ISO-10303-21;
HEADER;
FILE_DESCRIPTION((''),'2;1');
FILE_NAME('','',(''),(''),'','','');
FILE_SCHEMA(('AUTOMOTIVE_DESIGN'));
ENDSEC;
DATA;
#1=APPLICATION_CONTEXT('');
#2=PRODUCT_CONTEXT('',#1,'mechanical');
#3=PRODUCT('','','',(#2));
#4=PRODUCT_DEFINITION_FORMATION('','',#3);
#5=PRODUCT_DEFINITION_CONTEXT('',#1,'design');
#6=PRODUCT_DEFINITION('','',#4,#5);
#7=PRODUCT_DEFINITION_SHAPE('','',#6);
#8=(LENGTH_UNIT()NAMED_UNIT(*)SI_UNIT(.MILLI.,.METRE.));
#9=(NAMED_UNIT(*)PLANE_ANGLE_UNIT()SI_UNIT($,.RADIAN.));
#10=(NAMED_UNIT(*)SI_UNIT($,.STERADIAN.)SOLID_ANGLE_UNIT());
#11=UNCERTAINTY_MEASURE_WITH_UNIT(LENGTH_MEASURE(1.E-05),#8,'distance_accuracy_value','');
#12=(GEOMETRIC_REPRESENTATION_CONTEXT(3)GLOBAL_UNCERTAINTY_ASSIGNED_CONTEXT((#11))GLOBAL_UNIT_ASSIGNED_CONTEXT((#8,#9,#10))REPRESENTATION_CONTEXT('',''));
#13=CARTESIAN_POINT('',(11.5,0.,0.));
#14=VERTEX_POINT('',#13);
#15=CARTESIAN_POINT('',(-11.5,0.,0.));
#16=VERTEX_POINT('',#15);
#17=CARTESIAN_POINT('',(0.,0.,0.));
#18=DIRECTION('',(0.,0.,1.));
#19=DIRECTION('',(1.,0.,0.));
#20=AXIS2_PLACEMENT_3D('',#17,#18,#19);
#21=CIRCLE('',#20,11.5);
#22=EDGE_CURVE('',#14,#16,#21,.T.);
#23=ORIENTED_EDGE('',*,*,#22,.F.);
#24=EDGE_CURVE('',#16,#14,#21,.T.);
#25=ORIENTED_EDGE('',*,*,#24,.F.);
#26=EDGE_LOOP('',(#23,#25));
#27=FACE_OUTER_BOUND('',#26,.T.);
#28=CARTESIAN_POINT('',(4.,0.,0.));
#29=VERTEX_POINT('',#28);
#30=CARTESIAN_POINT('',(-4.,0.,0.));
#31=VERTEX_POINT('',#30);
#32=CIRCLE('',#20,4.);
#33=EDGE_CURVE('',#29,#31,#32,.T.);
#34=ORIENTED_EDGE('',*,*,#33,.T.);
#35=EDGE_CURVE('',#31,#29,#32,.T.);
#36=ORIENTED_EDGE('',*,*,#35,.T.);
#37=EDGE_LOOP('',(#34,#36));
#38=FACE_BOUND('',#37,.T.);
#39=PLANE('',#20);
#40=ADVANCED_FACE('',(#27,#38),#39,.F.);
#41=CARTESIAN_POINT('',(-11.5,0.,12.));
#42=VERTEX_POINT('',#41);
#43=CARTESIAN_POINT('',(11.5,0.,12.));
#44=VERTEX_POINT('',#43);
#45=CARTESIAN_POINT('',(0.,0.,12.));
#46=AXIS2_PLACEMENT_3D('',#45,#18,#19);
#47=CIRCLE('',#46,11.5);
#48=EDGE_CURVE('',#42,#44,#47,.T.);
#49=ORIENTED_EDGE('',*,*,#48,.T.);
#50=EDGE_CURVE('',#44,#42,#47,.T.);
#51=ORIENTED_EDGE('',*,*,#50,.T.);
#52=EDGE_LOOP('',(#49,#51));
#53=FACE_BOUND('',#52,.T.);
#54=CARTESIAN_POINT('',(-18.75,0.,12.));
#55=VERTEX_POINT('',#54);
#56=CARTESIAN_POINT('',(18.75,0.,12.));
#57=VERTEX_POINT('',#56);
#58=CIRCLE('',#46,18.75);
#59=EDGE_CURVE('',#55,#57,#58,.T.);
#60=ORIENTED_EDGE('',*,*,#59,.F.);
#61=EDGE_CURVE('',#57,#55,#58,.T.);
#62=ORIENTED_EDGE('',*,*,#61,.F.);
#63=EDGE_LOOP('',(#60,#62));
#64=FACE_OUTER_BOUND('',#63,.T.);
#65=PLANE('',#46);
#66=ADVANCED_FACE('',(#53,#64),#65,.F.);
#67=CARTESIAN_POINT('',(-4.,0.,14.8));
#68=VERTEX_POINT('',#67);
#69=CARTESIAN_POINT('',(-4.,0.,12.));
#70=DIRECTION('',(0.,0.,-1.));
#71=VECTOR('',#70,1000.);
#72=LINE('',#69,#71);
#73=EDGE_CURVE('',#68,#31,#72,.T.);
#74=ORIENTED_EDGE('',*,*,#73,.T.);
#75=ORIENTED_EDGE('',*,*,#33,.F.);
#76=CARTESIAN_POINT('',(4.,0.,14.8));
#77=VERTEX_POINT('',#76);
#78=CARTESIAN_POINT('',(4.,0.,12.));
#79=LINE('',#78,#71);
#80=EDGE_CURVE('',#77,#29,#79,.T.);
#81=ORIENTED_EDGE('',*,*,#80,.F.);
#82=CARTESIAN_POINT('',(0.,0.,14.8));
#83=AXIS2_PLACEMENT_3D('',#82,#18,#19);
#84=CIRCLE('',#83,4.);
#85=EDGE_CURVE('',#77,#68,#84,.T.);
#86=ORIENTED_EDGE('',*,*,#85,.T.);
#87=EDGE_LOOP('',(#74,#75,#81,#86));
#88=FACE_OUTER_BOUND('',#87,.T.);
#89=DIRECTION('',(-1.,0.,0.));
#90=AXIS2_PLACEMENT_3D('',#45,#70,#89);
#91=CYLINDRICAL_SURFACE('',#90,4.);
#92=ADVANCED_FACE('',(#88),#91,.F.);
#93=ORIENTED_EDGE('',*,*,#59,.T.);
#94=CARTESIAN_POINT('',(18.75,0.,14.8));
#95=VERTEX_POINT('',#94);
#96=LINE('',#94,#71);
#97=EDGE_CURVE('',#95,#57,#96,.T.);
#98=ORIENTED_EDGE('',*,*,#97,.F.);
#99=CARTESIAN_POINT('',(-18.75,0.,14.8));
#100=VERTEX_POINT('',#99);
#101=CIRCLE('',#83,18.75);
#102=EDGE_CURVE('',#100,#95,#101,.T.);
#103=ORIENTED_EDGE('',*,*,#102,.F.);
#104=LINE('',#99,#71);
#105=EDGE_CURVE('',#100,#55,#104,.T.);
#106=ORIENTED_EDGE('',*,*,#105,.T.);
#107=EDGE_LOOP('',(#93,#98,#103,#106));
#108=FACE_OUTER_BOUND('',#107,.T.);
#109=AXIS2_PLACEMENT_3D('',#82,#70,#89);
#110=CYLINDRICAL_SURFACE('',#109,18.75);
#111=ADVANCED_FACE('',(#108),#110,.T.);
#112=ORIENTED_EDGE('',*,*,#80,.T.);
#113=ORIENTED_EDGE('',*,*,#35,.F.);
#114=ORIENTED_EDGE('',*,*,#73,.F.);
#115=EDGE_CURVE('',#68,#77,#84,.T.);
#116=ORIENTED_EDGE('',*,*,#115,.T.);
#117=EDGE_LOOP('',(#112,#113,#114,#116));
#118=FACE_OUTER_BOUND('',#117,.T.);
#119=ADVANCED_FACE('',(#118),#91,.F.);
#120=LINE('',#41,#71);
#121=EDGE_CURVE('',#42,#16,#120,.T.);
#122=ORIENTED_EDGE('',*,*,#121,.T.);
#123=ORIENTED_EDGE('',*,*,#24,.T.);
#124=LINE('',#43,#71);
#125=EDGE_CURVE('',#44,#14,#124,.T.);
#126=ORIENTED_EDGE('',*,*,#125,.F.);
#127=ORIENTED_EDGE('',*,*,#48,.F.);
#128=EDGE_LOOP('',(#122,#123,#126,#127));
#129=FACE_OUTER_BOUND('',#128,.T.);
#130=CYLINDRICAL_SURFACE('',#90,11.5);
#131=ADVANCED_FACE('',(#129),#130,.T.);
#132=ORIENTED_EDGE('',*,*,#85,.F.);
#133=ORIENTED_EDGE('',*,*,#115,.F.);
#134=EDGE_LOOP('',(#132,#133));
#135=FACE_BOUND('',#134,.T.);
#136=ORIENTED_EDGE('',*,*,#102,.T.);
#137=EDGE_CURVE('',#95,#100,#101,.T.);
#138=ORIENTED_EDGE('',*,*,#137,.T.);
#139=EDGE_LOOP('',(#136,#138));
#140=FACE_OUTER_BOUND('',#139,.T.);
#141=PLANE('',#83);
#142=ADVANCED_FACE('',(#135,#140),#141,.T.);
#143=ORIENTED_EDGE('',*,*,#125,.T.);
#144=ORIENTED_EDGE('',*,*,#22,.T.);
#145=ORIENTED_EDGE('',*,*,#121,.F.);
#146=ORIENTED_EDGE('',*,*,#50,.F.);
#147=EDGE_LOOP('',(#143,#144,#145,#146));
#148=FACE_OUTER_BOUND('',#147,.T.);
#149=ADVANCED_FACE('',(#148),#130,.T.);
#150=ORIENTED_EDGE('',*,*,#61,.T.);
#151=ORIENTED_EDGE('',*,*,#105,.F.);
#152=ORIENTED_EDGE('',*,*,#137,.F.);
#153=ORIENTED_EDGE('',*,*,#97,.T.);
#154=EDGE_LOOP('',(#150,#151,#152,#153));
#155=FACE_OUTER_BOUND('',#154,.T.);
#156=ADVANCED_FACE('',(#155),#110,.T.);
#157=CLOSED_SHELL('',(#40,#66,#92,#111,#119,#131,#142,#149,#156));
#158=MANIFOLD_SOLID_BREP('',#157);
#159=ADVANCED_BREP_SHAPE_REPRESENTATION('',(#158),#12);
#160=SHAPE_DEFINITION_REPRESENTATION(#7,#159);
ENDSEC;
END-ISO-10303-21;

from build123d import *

# Parameters (mm, degrees)
SKETCH_1_R      = 11.5
SKETCH_1_R_2    = 4
EXTRUDE_1_DEPTH = 12
SKETCH_2_R      = 18.75
SKETCH_2_R_2    = 4
EXTRUDE_2_DEPTH = 2.8


with BuildPart() as part:
    # 草图1 → 凸台-拉伸1 (new body)
    with BuildSketch(Plane.XY):
        Circle(SKETCH_1_R)
        Circle(SKETCH_1_R_2, mode=Mode.SUBTRACT)
    extrude(amount=EXTRUDE_1_DEPTH)

    # 草图2 → 凸台-拉伸2 (add)
    with BuildSketch(Plane.XY.offset(12)):
        Circle(SKETCH_2_R)
        Circle(SKETCH_2_R_2, mode=Mode.SUBTRACT)
    extrude(amount=EXTRUDE_2_DEPTH)


solid = part.part
